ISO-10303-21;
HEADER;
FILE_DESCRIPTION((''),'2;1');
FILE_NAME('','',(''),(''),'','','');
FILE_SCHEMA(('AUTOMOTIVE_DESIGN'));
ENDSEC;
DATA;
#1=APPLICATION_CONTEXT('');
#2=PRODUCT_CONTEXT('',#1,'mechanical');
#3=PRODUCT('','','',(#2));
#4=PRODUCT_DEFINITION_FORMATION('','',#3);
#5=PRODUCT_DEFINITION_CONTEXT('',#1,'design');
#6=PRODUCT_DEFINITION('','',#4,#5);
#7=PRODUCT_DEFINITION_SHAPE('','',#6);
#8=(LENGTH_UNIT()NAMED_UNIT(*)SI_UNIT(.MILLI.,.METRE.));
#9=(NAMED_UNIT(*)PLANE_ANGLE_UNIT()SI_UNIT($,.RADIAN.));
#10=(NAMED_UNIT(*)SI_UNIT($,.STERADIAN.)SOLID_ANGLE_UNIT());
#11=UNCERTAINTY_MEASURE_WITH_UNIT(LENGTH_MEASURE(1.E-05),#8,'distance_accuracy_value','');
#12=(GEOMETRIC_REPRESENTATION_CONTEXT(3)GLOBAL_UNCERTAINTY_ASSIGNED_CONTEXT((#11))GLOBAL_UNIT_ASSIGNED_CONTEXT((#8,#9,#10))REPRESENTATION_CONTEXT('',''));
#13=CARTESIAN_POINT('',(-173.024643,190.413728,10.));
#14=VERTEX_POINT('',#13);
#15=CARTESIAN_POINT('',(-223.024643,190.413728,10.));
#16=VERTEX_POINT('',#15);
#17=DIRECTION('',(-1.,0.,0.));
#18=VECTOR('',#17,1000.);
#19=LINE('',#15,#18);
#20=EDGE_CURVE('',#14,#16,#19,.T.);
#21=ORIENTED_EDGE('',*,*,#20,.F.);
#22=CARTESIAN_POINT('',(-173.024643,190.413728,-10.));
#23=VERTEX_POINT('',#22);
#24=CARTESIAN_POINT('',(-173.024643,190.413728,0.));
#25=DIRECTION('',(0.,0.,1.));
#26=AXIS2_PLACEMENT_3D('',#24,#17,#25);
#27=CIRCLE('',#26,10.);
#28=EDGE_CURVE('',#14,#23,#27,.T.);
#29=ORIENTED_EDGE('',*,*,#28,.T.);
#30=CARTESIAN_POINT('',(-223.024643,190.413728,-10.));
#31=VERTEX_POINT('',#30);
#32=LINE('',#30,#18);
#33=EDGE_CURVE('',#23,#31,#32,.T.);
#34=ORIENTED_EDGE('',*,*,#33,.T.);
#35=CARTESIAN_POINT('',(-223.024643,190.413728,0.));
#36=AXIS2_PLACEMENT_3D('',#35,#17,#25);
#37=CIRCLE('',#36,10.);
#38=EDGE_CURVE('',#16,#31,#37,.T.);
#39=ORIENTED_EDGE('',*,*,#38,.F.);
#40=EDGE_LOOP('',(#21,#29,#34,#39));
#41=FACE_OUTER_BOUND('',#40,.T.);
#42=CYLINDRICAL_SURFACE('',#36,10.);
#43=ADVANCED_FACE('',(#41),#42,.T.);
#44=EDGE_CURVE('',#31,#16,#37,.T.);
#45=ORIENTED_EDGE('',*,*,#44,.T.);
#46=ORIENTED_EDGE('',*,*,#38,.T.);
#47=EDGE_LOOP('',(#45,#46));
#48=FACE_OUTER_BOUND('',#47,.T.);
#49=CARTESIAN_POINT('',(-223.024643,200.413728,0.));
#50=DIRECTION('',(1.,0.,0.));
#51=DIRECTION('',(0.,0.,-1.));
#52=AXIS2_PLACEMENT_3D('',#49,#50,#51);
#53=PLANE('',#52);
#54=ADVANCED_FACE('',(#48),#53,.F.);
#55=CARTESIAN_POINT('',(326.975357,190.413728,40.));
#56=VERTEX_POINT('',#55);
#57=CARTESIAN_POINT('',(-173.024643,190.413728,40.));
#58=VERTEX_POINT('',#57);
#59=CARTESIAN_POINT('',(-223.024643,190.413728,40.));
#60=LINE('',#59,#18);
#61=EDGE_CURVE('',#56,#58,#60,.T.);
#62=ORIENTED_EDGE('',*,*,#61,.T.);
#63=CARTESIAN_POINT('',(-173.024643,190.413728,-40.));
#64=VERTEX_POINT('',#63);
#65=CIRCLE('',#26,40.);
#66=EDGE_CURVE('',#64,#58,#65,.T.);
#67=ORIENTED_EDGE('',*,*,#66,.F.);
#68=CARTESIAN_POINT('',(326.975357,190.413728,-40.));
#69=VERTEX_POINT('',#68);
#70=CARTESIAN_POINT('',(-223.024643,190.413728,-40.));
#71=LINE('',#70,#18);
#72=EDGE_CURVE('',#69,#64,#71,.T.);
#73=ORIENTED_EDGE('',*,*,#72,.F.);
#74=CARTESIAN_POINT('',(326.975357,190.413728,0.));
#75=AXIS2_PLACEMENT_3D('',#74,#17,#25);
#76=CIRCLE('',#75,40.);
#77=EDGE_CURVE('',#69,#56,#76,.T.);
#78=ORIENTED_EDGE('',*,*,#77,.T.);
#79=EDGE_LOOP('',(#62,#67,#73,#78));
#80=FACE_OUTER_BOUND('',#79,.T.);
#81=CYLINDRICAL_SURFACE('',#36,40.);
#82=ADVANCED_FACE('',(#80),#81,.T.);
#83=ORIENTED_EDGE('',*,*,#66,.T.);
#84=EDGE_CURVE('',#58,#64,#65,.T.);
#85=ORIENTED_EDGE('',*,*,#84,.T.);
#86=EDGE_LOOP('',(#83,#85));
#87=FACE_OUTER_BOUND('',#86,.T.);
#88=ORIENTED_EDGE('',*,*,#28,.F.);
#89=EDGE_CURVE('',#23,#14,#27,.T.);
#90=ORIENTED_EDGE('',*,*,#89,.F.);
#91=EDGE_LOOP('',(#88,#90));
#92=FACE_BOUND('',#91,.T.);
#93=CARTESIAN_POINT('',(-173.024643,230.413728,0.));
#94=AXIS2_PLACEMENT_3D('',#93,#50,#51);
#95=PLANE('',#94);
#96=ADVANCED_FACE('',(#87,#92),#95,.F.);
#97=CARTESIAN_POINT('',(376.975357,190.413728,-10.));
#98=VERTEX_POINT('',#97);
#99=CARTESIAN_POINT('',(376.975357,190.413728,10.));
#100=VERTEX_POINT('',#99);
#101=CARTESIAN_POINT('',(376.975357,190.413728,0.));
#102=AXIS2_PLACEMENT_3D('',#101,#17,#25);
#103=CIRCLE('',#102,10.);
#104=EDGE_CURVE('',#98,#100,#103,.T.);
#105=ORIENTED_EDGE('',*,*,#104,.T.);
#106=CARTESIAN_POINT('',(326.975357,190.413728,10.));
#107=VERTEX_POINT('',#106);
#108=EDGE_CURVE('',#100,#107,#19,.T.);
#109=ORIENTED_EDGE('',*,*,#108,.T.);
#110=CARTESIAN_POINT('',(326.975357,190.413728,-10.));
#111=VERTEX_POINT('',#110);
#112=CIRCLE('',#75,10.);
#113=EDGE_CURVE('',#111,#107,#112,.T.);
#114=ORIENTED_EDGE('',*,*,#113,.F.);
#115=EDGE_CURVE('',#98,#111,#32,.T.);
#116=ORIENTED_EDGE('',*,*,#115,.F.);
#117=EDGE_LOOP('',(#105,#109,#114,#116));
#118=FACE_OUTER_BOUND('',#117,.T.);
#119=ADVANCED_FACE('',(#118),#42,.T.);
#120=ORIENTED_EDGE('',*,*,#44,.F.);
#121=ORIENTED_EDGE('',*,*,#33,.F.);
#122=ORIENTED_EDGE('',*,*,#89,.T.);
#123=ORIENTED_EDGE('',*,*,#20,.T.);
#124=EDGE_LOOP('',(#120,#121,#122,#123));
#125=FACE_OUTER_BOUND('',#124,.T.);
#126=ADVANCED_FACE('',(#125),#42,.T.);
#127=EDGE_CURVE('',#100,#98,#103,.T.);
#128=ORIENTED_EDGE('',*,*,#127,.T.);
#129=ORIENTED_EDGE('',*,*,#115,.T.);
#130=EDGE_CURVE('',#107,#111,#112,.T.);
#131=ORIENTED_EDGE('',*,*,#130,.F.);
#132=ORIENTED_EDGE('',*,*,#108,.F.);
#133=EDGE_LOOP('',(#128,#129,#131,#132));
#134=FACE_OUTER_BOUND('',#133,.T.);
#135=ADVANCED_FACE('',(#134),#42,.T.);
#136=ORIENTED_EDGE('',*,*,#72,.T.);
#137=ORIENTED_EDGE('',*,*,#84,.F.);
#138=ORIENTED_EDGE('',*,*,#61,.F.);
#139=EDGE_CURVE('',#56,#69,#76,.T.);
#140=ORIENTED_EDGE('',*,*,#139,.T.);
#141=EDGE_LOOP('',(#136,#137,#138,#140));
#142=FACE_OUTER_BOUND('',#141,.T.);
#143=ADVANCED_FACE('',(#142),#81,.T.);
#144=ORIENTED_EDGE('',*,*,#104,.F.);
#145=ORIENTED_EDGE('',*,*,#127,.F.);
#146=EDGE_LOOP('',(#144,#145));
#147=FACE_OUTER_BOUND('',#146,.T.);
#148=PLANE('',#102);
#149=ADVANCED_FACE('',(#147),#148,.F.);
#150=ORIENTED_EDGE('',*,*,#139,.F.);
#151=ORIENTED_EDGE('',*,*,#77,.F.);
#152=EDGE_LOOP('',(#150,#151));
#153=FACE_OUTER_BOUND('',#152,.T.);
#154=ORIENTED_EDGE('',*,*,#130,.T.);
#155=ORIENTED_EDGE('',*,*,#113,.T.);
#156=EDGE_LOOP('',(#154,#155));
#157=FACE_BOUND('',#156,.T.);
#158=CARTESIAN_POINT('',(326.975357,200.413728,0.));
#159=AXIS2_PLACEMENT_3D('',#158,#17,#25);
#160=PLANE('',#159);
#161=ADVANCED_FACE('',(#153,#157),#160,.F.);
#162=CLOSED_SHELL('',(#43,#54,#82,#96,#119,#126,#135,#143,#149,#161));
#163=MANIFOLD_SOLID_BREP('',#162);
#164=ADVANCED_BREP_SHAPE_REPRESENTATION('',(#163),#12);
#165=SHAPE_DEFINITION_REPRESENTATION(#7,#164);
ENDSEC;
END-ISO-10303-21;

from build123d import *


with BuildPart() as part:
    # Sketch1 → Revolve1 (revolve)
    with BuildSketch(Plane.XY, mode=Mode.PRIVATE) as revolve1_sk:
        Polygon((-223.024643435, 190.413727793), (376.975356565, 190.413727793), (376.975356565, 200.413727793), (326.975356565, 200.413727793), (326.975356565, 230.413727793), (-173.024643435, 230.413727793), (-173.024643435, 200.413727793), (-223.024643435, 200.413727793), align=None)
    revolve(revolve1_sk.sketch.rotate(Axis((-223.024643435, 190.413727793, 0), (1, 0, 0)), 90), axis=Axis((-223.024643435, 190.413727793, 0), (1, 0, 0)))


solid = part.part
